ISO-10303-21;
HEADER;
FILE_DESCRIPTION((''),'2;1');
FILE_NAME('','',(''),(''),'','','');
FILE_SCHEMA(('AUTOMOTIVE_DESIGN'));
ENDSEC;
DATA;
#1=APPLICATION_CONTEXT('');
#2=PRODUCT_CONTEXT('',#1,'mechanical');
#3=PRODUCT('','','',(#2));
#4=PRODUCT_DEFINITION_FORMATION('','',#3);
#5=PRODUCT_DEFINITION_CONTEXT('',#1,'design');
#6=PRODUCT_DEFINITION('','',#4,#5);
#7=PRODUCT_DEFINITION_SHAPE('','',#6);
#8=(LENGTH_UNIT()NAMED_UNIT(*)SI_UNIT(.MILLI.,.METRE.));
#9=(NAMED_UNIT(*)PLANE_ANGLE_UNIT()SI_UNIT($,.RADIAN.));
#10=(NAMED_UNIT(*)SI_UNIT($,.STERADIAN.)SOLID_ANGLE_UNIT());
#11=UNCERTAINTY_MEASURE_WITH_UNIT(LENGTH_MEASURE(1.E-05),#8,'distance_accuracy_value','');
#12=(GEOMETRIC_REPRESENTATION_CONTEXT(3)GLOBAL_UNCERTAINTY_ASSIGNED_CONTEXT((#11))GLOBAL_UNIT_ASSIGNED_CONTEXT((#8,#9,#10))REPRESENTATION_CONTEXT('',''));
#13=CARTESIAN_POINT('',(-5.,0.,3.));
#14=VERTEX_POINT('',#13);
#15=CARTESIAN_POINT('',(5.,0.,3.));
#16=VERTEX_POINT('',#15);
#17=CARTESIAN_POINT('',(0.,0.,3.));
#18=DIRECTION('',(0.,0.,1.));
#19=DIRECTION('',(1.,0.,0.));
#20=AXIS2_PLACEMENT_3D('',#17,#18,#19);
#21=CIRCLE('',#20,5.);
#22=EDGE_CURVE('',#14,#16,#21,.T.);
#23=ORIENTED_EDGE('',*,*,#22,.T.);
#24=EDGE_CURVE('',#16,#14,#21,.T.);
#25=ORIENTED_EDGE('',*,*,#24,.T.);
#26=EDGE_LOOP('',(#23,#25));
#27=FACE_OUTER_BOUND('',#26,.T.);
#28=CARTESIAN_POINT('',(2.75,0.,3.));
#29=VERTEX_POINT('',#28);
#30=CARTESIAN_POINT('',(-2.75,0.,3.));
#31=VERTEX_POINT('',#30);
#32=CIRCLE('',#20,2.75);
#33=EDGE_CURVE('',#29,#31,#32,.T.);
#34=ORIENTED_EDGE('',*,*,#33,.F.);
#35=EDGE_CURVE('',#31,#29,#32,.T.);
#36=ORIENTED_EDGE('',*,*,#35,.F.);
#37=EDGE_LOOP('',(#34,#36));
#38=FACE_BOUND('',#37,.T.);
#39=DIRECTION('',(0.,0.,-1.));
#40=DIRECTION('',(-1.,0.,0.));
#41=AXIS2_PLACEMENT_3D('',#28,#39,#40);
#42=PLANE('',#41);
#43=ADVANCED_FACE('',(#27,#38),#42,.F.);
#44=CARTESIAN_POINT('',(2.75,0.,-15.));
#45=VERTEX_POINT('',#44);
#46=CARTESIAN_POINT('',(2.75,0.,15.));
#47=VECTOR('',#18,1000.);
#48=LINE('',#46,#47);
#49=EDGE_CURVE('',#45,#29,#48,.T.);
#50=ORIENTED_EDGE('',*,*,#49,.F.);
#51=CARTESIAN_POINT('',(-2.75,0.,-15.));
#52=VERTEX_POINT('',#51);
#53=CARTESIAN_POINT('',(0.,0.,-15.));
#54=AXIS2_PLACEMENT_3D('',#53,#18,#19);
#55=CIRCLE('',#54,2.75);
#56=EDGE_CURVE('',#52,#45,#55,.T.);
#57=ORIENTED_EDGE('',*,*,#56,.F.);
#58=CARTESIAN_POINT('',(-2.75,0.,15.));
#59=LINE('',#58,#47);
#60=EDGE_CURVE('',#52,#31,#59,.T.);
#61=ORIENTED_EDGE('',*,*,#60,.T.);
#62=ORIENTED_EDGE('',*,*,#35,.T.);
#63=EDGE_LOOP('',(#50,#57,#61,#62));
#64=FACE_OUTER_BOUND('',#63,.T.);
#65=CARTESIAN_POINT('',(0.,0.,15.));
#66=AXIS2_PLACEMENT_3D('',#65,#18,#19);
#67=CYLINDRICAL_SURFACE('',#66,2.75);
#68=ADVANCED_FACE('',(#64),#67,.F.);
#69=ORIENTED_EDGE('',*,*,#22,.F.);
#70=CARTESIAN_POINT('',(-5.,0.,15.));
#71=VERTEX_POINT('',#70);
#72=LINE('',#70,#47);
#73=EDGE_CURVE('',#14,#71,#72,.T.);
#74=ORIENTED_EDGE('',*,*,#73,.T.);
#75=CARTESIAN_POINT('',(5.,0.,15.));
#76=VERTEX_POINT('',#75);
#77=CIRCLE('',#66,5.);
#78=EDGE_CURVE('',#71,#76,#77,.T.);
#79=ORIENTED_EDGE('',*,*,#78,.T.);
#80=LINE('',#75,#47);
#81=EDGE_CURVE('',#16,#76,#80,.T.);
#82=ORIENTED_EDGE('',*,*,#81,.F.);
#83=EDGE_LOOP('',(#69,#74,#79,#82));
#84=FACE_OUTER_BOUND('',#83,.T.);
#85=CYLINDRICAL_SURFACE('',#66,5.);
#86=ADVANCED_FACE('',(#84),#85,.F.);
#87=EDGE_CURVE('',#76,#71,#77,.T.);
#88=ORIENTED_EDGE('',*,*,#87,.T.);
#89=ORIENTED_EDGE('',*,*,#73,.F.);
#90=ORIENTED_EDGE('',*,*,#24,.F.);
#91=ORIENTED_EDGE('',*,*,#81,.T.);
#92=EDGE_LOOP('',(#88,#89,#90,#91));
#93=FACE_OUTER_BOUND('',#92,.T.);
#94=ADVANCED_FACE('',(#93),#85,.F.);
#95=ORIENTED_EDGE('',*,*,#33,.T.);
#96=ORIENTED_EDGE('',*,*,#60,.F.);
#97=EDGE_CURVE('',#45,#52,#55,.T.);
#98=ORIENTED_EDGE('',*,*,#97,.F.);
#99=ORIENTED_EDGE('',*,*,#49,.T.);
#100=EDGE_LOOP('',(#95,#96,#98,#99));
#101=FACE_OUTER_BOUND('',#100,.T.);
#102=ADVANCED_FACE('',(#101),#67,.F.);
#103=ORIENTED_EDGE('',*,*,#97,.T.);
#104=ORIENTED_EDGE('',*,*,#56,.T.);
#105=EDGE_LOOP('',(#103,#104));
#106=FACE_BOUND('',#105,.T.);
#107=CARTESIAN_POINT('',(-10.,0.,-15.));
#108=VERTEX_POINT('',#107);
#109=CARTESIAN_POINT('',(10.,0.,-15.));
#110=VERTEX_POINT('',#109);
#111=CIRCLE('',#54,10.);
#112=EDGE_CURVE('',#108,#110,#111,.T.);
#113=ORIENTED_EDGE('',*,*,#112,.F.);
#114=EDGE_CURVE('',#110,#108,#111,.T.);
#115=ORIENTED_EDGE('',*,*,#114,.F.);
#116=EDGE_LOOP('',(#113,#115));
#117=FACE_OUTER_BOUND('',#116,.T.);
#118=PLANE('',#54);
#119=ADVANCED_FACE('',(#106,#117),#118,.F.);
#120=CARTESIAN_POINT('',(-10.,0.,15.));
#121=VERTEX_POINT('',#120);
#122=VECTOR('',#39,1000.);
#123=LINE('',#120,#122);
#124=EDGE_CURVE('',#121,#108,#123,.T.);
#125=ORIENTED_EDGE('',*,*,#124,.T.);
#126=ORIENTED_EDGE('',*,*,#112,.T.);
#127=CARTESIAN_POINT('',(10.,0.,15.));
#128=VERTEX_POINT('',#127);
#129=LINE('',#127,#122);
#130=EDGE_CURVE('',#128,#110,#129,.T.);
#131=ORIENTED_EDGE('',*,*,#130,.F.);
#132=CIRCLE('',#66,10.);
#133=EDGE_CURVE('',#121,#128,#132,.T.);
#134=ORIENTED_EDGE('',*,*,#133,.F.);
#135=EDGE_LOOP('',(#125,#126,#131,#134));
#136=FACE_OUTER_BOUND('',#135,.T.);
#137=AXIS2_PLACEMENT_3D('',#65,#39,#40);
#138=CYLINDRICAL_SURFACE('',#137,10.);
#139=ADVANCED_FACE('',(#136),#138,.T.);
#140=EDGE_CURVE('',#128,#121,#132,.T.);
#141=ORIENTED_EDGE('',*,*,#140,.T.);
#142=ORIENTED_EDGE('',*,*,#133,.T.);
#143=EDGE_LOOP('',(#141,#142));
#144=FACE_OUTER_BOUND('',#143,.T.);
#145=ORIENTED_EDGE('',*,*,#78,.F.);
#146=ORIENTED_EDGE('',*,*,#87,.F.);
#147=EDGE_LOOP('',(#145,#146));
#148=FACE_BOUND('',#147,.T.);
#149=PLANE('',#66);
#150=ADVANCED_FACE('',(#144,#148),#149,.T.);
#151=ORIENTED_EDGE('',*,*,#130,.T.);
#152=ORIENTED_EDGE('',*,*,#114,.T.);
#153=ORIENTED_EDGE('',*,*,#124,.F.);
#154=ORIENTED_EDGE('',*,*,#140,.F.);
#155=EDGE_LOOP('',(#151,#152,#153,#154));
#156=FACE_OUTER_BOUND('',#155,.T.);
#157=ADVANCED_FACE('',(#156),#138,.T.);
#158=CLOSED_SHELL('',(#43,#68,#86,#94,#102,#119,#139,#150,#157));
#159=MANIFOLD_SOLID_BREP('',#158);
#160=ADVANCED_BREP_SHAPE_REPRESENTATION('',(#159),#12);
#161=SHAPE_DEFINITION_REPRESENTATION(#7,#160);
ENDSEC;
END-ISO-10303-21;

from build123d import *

# Parameters (mm, degrees)
SKETCH_1_R                = 10
EXTRUDE_1_DEPTH           = 15
HOLE_WIZARD_1_D           = 5.5
HOLE_WIZARD_1_CBORE_D     = 10
HOLE_WIZARD_1_CBORE_DEPTH = 12


with BuildPart() as part:
    # 草图1 → 凸台-拉伸1 (new, symmetric)
    with BuildSketch(Plane.XY):
        Circle(SKETCH_1_R)
    extrude(amount=EXTRUDE_1_DEPTH, both=True)

    # 打孔尺寸(%根据)内六角圆柱头螺钉的类型1 (through all)
    with Locations(Plane.XY.offset(15)):
        with Locations((0, 0)):
            CounterBoreHole(HOLE_WIZARD_1_D / 2, HOLE_WIZARD_1_CBORE_D / 2, HOLE_WIZARD_1_CBORE_DEPTH)


solid = part.part
